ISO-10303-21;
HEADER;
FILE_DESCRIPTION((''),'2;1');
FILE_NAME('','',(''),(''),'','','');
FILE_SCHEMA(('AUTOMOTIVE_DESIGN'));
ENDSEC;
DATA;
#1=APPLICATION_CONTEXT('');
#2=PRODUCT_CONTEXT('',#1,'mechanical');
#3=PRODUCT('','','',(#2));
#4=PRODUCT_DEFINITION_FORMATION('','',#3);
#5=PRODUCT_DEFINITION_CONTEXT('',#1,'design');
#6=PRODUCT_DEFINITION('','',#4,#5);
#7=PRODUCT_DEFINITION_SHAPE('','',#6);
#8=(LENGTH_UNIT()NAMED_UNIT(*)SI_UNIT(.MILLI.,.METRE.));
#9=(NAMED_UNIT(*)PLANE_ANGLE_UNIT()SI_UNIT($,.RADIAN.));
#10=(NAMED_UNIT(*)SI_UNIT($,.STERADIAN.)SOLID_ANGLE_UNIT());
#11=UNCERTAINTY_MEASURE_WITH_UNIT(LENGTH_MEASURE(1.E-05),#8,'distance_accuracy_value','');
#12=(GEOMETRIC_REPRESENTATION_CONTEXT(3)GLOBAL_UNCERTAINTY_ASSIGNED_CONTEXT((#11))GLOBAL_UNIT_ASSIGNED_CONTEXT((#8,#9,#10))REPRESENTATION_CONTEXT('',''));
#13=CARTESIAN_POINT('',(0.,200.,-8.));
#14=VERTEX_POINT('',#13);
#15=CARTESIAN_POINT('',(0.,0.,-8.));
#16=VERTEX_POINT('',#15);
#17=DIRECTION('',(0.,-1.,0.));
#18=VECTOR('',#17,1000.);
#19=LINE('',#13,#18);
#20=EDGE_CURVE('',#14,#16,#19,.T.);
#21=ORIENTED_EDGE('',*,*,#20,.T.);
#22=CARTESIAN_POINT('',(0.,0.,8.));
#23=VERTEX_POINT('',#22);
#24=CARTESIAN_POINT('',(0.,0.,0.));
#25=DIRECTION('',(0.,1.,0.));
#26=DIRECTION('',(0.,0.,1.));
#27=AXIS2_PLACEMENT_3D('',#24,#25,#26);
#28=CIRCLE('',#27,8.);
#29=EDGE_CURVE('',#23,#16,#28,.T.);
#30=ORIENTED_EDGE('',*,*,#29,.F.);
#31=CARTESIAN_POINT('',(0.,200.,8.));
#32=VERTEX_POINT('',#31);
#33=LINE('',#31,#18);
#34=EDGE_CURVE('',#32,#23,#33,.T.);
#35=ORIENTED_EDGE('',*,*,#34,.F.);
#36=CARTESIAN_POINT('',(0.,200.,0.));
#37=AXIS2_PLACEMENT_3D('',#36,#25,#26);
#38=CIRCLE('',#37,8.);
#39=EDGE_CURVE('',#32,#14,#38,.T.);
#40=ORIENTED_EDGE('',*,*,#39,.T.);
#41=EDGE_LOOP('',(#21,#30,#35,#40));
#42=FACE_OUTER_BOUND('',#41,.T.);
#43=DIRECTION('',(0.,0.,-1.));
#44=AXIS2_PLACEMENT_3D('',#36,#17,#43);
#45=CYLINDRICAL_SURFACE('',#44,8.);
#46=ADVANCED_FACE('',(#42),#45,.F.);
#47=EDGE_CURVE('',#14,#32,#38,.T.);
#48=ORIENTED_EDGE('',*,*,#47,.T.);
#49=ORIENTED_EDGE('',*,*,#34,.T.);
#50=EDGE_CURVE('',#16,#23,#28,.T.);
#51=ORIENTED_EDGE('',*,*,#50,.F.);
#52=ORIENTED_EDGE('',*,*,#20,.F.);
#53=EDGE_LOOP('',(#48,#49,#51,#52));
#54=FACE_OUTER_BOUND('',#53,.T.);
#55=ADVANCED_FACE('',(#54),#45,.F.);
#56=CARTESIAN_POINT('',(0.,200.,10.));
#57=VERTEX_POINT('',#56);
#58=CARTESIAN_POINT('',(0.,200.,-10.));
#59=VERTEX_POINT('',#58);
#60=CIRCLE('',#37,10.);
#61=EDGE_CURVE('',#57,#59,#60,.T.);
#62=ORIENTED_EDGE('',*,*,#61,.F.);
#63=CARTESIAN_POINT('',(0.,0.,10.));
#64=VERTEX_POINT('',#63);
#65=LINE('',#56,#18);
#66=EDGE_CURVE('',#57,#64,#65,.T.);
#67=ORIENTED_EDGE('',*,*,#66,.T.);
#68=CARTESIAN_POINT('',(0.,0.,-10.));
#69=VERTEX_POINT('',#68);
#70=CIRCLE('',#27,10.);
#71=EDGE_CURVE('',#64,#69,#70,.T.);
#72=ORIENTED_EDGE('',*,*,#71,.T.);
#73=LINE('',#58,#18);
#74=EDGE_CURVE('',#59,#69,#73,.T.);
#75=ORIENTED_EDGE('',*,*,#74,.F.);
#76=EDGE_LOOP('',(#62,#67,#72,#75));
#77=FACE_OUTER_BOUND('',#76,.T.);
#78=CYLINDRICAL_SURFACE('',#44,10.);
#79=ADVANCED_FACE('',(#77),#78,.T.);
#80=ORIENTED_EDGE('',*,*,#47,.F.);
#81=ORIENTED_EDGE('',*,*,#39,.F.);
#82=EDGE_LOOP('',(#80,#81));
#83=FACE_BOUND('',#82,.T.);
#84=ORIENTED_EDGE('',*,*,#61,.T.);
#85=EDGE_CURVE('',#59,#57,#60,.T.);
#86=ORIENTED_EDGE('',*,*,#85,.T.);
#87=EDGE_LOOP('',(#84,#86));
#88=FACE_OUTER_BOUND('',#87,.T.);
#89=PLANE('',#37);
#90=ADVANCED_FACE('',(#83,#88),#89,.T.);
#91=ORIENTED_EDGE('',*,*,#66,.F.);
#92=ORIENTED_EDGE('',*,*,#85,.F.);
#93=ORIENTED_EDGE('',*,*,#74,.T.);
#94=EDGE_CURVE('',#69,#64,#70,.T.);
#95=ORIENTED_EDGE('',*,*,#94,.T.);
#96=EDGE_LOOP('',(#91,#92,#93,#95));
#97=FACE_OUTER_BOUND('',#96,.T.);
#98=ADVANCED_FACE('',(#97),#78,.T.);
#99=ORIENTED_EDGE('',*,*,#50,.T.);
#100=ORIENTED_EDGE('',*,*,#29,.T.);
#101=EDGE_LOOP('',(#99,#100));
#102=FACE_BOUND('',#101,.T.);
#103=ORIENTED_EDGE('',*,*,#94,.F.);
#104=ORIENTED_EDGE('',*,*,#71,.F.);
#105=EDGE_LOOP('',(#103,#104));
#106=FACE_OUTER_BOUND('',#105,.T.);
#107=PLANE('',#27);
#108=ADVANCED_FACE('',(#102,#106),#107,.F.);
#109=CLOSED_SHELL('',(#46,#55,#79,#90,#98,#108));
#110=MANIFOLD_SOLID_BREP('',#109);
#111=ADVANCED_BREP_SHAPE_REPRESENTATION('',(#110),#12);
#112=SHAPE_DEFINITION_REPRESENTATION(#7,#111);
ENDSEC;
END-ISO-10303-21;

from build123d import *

# Parameters (mm, degrees)
SKETCH11_R                             = 10
SKETCH11_R_2                           = 8
GB_T_6728_2002_ROUND_TUBE_20_2_1_DEPTH = 200


with BuildPart() as part:
    # Sketch11 → GB/T 6728-2002 round tube 20 × 2(1) (new body)
    with BuildSketch(Plane(origin=(0, 0, 0), x_dir=(-1, 0, 0), z_dir=(0, 1, 0))):
        Circle(SKETCH11_R)
        Circle(SKETCH11_R_2, mode=Mode.SUBTRACT)
    extrude(amount=GB_T_6728_2002_ROUND_TUBE_20_2_1_DEPTH)


solid = part.part
